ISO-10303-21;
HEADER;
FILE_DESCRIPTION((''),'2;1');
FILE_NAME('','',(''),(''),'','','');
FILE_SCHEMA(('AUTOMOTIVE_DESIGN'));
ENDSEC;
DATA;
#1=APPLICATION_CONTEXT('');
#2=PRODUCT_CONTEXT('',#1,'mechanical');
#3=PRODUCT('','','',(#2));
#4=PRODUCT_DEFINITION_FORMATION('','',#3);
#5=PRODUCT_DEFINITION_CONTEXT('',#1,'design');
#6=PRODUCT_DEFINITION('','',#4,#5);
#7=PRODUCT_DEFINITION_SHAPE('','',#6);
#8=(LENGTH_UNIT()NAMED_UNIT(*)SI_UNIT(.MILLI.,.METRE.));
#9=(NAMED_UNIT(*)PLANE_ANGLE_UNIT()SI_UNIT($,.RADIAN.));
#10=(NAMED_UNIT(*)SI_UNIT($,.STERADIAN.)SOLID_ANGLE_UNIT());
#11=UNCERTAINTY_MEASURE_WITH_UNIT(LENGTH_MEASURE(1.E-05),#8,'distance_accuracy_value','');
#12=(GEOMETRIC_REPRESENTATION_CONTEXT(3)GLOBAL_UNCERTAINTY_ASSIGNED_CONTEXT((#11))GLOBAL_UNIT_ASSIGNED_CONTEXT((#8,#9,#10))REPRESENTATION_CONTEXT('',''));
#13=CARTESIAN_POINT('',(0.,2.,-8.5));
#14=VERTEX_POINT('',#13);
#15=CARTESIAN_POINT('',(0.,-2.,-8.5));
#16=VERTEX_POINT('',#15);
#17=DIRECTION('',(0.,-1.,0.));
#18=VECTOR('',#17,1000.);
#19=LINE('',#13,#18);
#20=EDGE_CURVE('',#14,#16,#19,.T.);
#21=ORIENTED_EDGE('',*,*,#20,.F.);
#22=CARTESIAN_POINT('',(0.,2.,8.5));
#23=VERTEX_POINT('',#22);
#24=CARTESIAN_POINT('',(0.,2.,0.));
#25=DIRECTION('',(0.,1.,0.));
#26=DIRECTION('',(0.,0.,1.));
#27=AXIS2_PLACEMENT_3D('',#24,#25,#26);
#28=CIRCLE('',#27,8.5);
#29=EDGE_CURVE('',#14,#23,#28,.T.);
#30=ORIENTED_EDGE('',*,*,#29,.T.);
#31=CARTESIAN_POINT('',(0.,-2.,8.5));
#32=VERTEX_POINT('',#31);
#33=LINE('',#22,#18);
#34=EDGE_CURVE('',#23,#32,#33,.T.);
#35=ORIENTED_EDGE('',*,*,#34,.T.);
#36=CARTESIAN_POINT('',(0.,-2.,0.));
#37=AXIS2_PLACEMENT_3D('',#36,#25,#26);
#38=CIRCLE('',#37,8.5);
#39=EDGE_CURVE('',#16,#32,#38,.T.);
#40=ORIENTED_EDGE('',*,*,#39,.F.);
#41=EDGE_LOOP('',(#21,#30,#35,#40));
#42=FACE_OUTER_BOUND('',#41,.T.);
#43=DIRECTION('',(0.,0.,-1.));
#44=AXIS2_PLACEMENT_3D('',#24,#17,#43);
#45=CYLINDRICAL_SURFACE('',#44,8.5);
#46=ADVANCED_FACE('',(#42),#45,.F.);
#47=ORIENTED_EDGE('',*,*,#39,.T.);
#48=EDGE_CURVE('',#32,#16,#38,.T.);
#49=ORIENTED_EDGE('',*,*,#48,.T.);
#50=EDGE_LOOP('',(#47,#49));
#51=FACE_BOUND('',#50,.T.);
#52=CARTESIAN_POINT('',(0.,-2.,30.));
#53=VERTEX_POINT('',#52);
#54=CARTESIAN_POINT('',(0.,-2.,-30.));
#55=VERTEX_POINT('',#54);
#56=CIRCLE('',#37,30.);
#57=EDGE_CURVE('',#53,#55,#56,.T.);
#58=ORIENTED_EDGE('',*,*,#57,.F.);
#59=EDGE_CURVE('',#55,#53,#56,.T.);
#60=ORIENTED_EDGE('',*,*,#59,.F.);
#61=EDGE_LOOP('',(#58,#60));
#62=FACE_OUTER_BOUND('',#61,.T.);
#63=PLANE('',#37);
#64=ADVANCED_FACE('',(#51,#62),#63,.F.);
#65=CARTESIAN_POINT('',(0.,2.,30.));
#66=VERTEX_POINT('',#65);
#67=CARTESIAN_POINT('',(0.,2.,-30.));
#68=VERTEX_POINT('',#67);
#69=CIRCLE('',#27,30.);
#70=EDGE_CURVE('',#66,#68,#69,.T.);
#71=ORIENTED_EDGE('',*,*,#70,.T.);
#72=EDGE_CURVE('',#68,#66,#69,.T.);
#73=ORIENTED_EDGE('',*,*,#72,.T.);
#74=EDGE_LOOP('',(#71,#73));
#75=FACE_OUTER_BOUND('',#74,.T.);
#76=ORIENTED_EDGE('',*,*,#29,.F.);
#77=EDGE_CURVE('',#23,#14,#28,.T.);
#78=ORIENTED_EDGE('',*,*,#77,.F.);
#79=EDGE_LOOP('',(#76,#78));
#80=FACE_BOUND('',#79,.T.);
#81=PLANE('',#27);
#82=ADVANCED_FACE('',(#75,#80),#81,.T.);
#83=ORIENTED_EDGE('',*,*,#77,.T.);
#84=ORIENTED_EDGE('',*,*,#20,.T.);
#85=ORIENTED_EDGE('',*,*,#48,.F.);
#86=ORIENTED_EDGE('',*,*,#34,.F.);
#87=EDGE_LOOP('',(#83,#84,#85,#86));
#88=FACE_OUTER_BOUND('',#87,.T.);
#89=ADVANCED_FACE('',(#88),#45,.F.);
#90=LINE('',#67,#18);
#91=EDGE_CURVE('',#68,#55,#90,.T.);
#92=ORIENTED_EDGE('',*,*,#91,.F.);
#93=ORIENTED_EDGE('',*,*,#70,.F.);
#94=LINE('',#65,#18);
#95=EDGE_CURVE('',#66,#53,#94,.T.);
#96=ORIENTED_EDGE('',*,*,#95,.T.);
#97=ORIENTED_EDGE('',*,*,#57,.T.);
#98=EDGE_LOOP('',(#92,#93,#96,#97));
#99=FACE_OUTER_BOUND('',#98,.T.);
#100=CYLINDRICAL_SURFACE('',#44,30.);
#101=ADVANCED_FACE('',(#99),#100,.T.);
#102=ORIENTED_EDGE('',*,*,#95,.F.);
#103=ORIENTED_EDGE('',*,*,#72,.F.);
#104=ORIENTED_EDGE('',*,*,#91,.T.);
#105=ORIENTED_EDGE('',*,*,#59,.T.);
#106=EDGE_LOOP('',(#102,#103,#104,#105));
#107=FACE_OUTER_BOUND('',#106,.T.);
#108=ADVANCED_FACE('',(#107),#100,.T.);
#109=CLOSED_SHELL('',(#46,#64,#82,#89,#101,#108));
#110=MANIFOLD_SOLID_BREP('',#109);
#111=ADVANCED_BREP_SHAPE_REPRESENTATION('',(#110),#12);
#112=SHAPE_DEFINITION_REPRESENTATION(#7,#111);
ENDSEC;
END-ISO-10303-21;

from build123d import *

# Parameters (mm, degrees)
SKETCH1_R      = 30
SKETCH1_R_2    = 8.5
EXTRUDE1_DEPTH = 2


with BuildPart() as part:
    # Sketch1 → Extrude1 (new, symmetric)
    with BuildSketch(Plane(origin=(0, 0, 0), x_dir=(1, 0, 0), z_dir=(0, 1, 0))):
        with Locations(Location((0, 0, 0), (0, 0, 270))):
            Circle(SKETCH1_R)
        with Locations(Location((0, 0, 0), (0, 0, 270))):
            Circle(SKETCH1_R_2, mode=Mode.SUBTRACT)
    extrude(amount=EXTRUDE1_DEPTH, both=True)


solid = part.part
